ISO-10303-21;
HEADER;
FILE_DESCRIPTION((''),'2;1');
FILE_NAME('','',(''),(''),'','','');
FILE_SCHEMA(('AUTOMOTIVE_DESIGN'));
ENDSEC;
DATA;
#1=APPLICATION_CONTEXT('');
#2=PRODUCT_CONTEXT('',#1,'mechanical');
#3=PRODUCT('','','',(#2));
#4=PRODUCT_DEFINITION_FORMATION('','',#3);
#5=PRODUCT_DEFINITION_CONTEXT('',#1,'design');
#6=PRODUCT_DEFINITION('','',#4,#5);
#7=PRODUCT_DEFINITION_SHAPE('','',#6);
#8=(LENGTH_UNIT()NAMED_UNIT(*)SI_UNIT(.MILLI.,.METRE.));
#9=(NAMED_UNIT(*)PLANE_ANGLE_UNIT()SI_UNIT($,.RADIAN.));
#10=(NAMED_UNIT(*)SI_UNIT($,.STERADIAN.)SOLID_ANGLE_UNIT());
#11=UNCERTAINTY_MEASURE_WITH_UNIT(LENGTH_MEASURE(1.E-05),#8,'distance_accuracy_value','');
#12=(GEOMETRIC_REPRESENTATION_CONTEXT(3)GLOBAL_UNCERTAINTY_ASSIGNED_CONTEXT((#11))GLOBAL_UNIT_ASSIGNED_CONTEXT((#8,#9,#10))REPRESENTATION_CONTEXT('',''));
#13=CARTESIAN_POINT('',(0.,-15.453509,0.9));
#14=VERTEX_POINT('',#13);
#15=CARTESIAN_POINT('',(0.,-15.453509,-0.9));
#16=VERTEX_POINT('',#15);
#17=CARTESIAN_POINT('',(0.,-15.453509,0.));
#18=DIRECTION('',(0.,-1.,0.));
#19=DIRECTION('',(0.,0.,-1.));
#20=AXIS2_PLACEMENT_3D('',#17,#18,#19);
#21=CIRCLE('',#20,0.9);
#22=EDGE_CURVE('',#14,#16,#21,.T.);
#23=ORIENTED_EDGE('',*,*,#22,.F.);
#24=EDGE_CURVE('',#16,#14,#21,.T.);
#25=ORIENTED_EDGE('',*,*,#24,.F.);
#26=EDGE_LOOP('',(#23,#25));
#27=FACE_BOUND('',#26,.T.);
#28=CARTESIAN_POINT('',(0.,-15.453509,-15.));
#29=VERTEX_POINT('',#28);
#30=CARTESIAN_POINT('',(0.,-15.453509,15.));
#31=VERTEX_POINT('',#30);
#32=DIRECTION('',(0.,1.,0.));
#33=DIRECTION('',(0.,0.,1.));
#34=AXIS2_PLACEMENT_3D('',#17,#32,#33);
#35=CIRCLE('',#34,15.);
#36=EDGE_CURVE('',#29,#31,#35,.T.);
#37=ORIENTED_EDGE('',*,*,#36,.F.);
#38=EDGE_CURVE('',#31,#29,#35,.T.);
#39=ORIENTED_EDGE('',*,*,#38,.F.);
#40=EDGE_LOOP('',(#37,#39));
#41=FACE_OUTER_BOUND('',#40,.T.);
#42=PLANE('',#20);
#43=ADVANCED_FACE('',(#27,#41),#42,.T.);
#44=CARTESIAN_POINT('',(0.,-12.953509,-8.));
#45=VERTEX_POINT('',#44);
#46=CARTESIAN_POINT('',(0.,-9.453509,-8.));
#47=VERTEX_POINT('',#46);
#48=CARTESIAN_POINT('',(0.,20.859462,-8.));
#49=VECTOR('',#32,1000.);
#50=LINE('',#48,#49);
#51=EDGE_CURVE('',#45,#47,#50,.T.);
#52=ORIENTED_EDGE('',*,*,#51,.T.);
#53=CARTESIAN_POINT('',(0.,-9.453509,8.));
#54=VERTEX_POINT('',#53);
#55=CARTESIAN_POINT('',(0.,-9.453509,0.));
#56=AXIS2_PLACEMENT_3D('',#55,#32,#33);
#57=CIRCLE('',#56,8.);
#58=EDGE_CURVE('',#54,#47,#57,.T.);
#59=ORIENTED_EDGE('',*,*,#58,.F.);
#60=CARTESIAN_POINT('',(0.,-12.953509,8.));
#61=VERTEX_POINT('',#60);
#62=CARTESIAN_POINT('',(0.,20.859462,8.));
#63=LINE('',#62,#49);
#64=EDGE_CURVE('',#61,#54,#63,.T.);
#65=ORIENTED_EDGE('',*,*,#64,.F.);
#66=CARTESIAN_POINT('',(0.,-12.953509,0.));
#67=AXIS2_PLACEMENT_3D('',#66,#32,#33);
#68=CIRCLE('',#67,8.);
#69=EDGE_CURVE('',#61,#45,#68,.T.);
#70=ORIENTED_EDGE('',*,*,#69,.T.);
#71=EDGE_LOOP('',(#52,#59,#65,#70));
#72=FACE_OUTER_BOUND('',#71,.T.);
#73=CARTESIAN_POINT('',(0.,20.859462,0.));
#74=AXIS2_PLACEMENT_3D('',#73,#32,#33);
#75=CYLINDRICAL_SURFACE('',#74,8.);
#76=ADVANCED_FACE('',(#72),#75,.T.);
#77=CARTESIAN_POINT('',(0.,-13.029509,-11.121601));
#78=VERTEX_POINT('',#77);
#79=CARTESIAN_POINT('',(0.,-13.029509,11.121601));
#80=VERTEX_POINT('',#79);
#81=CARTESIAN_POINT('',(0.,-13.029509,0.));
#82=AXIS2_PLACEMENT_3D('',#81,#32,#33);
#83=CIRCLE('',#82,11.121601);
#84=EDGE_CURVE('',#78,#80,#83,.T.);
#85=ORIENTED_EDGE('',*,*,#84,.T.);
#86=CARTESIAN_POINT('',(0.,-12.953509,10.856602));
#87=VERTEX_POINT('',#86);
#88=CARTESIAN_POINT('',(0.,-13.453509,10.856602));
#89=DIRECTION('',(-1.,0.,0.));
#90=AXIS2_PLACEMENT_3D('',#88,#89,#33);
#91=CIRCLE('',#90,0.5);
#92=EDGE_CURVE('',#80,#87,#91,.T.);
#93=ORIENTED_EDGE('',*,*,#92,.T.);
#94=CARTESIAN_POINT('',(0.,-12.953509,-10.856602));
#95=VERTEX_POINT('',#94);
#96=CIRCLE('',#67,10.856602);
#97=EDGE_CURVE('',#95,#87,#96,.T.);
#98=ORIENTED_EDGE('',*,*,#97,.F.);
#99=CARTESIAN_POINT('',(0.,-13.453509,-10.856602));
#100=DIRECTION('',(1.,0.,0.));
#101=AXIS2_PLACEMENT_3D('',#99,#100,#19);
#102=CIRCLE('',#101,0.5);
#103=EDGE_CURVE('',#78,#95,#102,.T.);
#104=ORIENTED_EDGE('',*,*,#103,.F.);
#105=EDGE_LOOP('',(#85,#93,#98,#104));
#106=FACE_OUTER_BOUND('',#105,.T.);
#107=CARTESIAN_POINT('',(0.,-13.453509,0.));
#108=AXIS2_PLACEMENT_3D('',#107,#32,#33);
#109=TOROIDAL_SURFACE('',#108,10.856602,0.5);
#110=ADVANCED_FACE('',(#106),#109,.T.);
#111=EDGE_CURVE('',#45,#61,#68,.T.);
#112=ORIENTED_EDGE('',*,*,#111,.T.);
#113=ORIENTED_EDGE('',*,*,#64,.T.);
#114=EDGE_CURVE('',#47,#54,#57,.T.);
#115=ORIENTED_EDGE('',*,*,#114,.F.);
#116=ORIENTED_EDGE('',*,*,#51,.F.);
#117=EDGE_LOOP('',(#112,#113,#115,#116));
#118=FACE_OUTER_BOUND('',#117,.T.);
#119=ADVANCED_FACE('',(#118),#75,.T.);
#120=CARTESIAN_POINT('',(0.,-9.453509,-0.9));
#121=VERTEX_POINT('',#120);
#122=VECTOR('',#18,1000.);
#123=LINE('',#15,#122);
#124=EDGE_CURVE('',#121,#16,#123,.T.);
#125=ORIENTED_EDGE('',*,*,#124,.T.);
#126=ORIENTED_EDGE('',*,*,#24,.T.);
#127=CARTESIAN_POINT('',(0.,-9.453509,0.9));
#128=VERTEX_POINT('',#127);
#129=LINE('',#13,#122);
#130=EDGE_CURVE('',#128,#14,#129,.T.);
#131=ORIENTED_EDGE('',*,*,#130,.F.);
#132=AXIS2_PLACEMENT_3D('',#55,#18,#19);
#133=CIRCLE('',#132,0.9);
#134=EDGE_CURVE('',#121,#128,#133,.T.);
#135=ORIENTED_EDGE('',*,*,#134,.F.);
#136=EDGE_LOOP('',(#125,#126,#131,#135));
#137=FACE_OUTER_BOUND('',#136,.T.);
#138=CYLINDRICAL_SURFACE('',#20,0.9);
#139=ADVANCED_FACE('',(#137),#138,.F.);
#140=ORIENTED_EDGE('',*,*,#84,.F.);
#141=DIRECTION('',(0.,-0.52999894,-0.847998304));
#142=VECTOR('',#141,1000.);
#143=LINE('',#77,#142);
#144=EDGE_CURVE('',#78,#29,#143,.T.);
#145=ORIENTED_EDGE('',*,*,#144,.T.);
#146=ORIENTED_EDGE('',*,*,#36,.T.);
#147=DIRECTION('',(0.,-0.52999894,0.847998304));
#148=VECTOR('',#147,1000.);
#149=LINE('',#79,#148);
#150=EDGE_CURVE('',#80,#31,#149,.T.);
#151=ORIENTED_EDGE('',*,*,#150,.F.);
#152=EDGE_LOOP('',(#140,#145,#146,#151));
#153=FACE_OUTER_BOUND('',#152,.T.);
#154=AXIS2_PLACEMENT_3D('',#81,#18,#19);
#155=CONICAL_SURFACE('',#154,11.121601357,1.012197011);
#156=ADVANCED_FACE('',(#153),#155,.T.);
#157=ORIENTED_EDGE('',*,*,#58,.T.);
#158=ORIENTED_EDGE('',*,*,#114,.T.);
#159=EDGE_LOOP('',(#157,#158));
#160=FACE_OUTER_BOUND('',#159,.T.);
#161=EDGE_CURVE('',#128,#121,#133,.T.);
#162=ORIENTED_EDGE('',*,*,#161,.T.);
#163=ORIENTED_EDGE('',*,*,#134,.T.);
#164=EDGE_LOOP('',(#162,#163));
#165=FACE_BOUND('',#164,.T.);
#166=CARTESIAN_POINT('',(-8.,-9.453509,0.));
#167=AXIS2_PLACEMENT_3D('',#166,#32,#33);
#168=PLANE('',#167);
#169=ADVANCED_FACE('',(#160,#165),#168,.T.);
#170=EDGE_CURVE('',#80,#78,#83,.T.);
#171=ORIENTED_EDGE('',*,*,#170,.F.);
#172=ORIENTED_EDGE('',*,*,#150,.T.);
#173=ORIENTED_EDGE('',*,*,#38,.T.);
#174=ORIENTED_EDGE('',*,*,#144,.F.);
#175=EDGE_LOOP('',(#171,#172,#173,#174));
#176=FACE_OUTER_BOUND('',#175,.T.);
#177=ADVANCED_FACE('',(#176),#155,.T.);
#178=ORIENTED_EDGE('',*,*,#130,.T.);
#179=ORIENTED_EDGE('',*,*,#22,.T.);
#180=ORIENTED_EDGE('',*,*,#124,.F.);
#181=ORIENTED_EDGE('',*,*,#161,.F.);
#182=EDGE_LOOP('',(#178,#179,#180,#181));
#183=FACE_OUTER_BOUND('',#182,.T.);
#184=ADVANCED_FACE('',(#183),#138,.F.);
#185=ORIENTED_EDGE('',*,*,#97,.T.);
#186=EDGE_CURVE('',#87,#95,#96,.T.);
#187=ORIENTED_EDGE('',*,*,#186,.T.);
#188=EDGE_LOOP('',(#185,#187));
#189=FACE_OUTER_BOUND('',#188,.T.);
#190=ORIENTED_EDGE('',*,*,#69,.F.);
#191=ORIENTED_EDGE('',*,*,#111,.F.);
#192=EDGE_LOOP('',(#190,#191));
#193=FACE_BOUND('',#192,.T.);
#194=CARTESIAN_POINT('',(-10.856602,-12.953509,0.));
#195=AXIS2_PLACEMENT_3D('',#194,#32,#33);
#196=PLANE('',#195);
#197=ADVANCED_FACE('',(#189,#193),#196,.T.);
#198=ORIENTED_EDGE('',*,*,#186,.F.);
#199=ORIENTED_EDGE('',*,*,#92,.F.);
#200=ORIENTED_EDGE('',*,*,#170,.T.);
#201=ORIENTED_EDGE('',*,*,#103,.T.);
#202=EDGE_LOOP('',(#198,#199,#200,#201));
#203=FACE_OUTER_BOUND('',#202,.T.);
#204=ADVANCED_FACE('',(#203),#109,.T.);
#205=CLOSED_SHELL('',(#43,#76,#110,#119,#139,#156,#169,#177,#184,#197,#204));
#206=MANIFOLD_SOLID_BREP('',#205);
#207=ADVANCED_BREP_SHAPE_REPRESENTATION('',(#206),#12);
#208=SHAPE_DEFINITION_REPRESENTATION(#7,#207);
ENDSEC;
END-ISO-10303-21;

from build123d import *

# Parameters (mm, degrees)
CLEARANCE_HOLE_FOR_M1_62_D = 1.8


with BuildPart() as part:
    # Sketch1 → Revolution1 (revolve)
    with BuildSketch(Plane.XY, mode=Mode.PRIVATE) as revolution1_sk:
        with BuildLine():
            Line((0, -15.453508628), (-15, -15.453508628))
            Line((-15, -15.453508628), (-11.121601357, -13.029509476))
            ThreePointArc((-11.121601357, -13.029509476), (-10.994443143, -12.972884255), (-10.856601887, -12.953508628))
            Line((-10.856601887, -12.953508628), (-8, -12.953508628))
            Line((-8, -12.953508628), (-8, -11.453508628))
            Line((-8, -11.453508628), (-8, -9.453508628))
            Line((-8, -9.453508628), (0, -9.453508628))
            Line((0, -9.453508628), (0, -15.453508628))
        make_face()
    revolve(revolution1_sk.sketch.rotate(Axis((0, 20.85946169, 0), (0, -1, 0)), 270), axis=Axis((0, 20.85946169, 0), (0, -1, 0)))

    # Clearance hole for M1.62 (through all)
    with Locations(Plane(origin=(0, -15.453508628, 0), x_dir=(-1, 0, 0), z_dir=(0, -1, 0))):
        with Locations((0, 0)):
            Hole(CLEARANCE_HOLE_FOR_M1_62_D / 2)


solid = part.part
